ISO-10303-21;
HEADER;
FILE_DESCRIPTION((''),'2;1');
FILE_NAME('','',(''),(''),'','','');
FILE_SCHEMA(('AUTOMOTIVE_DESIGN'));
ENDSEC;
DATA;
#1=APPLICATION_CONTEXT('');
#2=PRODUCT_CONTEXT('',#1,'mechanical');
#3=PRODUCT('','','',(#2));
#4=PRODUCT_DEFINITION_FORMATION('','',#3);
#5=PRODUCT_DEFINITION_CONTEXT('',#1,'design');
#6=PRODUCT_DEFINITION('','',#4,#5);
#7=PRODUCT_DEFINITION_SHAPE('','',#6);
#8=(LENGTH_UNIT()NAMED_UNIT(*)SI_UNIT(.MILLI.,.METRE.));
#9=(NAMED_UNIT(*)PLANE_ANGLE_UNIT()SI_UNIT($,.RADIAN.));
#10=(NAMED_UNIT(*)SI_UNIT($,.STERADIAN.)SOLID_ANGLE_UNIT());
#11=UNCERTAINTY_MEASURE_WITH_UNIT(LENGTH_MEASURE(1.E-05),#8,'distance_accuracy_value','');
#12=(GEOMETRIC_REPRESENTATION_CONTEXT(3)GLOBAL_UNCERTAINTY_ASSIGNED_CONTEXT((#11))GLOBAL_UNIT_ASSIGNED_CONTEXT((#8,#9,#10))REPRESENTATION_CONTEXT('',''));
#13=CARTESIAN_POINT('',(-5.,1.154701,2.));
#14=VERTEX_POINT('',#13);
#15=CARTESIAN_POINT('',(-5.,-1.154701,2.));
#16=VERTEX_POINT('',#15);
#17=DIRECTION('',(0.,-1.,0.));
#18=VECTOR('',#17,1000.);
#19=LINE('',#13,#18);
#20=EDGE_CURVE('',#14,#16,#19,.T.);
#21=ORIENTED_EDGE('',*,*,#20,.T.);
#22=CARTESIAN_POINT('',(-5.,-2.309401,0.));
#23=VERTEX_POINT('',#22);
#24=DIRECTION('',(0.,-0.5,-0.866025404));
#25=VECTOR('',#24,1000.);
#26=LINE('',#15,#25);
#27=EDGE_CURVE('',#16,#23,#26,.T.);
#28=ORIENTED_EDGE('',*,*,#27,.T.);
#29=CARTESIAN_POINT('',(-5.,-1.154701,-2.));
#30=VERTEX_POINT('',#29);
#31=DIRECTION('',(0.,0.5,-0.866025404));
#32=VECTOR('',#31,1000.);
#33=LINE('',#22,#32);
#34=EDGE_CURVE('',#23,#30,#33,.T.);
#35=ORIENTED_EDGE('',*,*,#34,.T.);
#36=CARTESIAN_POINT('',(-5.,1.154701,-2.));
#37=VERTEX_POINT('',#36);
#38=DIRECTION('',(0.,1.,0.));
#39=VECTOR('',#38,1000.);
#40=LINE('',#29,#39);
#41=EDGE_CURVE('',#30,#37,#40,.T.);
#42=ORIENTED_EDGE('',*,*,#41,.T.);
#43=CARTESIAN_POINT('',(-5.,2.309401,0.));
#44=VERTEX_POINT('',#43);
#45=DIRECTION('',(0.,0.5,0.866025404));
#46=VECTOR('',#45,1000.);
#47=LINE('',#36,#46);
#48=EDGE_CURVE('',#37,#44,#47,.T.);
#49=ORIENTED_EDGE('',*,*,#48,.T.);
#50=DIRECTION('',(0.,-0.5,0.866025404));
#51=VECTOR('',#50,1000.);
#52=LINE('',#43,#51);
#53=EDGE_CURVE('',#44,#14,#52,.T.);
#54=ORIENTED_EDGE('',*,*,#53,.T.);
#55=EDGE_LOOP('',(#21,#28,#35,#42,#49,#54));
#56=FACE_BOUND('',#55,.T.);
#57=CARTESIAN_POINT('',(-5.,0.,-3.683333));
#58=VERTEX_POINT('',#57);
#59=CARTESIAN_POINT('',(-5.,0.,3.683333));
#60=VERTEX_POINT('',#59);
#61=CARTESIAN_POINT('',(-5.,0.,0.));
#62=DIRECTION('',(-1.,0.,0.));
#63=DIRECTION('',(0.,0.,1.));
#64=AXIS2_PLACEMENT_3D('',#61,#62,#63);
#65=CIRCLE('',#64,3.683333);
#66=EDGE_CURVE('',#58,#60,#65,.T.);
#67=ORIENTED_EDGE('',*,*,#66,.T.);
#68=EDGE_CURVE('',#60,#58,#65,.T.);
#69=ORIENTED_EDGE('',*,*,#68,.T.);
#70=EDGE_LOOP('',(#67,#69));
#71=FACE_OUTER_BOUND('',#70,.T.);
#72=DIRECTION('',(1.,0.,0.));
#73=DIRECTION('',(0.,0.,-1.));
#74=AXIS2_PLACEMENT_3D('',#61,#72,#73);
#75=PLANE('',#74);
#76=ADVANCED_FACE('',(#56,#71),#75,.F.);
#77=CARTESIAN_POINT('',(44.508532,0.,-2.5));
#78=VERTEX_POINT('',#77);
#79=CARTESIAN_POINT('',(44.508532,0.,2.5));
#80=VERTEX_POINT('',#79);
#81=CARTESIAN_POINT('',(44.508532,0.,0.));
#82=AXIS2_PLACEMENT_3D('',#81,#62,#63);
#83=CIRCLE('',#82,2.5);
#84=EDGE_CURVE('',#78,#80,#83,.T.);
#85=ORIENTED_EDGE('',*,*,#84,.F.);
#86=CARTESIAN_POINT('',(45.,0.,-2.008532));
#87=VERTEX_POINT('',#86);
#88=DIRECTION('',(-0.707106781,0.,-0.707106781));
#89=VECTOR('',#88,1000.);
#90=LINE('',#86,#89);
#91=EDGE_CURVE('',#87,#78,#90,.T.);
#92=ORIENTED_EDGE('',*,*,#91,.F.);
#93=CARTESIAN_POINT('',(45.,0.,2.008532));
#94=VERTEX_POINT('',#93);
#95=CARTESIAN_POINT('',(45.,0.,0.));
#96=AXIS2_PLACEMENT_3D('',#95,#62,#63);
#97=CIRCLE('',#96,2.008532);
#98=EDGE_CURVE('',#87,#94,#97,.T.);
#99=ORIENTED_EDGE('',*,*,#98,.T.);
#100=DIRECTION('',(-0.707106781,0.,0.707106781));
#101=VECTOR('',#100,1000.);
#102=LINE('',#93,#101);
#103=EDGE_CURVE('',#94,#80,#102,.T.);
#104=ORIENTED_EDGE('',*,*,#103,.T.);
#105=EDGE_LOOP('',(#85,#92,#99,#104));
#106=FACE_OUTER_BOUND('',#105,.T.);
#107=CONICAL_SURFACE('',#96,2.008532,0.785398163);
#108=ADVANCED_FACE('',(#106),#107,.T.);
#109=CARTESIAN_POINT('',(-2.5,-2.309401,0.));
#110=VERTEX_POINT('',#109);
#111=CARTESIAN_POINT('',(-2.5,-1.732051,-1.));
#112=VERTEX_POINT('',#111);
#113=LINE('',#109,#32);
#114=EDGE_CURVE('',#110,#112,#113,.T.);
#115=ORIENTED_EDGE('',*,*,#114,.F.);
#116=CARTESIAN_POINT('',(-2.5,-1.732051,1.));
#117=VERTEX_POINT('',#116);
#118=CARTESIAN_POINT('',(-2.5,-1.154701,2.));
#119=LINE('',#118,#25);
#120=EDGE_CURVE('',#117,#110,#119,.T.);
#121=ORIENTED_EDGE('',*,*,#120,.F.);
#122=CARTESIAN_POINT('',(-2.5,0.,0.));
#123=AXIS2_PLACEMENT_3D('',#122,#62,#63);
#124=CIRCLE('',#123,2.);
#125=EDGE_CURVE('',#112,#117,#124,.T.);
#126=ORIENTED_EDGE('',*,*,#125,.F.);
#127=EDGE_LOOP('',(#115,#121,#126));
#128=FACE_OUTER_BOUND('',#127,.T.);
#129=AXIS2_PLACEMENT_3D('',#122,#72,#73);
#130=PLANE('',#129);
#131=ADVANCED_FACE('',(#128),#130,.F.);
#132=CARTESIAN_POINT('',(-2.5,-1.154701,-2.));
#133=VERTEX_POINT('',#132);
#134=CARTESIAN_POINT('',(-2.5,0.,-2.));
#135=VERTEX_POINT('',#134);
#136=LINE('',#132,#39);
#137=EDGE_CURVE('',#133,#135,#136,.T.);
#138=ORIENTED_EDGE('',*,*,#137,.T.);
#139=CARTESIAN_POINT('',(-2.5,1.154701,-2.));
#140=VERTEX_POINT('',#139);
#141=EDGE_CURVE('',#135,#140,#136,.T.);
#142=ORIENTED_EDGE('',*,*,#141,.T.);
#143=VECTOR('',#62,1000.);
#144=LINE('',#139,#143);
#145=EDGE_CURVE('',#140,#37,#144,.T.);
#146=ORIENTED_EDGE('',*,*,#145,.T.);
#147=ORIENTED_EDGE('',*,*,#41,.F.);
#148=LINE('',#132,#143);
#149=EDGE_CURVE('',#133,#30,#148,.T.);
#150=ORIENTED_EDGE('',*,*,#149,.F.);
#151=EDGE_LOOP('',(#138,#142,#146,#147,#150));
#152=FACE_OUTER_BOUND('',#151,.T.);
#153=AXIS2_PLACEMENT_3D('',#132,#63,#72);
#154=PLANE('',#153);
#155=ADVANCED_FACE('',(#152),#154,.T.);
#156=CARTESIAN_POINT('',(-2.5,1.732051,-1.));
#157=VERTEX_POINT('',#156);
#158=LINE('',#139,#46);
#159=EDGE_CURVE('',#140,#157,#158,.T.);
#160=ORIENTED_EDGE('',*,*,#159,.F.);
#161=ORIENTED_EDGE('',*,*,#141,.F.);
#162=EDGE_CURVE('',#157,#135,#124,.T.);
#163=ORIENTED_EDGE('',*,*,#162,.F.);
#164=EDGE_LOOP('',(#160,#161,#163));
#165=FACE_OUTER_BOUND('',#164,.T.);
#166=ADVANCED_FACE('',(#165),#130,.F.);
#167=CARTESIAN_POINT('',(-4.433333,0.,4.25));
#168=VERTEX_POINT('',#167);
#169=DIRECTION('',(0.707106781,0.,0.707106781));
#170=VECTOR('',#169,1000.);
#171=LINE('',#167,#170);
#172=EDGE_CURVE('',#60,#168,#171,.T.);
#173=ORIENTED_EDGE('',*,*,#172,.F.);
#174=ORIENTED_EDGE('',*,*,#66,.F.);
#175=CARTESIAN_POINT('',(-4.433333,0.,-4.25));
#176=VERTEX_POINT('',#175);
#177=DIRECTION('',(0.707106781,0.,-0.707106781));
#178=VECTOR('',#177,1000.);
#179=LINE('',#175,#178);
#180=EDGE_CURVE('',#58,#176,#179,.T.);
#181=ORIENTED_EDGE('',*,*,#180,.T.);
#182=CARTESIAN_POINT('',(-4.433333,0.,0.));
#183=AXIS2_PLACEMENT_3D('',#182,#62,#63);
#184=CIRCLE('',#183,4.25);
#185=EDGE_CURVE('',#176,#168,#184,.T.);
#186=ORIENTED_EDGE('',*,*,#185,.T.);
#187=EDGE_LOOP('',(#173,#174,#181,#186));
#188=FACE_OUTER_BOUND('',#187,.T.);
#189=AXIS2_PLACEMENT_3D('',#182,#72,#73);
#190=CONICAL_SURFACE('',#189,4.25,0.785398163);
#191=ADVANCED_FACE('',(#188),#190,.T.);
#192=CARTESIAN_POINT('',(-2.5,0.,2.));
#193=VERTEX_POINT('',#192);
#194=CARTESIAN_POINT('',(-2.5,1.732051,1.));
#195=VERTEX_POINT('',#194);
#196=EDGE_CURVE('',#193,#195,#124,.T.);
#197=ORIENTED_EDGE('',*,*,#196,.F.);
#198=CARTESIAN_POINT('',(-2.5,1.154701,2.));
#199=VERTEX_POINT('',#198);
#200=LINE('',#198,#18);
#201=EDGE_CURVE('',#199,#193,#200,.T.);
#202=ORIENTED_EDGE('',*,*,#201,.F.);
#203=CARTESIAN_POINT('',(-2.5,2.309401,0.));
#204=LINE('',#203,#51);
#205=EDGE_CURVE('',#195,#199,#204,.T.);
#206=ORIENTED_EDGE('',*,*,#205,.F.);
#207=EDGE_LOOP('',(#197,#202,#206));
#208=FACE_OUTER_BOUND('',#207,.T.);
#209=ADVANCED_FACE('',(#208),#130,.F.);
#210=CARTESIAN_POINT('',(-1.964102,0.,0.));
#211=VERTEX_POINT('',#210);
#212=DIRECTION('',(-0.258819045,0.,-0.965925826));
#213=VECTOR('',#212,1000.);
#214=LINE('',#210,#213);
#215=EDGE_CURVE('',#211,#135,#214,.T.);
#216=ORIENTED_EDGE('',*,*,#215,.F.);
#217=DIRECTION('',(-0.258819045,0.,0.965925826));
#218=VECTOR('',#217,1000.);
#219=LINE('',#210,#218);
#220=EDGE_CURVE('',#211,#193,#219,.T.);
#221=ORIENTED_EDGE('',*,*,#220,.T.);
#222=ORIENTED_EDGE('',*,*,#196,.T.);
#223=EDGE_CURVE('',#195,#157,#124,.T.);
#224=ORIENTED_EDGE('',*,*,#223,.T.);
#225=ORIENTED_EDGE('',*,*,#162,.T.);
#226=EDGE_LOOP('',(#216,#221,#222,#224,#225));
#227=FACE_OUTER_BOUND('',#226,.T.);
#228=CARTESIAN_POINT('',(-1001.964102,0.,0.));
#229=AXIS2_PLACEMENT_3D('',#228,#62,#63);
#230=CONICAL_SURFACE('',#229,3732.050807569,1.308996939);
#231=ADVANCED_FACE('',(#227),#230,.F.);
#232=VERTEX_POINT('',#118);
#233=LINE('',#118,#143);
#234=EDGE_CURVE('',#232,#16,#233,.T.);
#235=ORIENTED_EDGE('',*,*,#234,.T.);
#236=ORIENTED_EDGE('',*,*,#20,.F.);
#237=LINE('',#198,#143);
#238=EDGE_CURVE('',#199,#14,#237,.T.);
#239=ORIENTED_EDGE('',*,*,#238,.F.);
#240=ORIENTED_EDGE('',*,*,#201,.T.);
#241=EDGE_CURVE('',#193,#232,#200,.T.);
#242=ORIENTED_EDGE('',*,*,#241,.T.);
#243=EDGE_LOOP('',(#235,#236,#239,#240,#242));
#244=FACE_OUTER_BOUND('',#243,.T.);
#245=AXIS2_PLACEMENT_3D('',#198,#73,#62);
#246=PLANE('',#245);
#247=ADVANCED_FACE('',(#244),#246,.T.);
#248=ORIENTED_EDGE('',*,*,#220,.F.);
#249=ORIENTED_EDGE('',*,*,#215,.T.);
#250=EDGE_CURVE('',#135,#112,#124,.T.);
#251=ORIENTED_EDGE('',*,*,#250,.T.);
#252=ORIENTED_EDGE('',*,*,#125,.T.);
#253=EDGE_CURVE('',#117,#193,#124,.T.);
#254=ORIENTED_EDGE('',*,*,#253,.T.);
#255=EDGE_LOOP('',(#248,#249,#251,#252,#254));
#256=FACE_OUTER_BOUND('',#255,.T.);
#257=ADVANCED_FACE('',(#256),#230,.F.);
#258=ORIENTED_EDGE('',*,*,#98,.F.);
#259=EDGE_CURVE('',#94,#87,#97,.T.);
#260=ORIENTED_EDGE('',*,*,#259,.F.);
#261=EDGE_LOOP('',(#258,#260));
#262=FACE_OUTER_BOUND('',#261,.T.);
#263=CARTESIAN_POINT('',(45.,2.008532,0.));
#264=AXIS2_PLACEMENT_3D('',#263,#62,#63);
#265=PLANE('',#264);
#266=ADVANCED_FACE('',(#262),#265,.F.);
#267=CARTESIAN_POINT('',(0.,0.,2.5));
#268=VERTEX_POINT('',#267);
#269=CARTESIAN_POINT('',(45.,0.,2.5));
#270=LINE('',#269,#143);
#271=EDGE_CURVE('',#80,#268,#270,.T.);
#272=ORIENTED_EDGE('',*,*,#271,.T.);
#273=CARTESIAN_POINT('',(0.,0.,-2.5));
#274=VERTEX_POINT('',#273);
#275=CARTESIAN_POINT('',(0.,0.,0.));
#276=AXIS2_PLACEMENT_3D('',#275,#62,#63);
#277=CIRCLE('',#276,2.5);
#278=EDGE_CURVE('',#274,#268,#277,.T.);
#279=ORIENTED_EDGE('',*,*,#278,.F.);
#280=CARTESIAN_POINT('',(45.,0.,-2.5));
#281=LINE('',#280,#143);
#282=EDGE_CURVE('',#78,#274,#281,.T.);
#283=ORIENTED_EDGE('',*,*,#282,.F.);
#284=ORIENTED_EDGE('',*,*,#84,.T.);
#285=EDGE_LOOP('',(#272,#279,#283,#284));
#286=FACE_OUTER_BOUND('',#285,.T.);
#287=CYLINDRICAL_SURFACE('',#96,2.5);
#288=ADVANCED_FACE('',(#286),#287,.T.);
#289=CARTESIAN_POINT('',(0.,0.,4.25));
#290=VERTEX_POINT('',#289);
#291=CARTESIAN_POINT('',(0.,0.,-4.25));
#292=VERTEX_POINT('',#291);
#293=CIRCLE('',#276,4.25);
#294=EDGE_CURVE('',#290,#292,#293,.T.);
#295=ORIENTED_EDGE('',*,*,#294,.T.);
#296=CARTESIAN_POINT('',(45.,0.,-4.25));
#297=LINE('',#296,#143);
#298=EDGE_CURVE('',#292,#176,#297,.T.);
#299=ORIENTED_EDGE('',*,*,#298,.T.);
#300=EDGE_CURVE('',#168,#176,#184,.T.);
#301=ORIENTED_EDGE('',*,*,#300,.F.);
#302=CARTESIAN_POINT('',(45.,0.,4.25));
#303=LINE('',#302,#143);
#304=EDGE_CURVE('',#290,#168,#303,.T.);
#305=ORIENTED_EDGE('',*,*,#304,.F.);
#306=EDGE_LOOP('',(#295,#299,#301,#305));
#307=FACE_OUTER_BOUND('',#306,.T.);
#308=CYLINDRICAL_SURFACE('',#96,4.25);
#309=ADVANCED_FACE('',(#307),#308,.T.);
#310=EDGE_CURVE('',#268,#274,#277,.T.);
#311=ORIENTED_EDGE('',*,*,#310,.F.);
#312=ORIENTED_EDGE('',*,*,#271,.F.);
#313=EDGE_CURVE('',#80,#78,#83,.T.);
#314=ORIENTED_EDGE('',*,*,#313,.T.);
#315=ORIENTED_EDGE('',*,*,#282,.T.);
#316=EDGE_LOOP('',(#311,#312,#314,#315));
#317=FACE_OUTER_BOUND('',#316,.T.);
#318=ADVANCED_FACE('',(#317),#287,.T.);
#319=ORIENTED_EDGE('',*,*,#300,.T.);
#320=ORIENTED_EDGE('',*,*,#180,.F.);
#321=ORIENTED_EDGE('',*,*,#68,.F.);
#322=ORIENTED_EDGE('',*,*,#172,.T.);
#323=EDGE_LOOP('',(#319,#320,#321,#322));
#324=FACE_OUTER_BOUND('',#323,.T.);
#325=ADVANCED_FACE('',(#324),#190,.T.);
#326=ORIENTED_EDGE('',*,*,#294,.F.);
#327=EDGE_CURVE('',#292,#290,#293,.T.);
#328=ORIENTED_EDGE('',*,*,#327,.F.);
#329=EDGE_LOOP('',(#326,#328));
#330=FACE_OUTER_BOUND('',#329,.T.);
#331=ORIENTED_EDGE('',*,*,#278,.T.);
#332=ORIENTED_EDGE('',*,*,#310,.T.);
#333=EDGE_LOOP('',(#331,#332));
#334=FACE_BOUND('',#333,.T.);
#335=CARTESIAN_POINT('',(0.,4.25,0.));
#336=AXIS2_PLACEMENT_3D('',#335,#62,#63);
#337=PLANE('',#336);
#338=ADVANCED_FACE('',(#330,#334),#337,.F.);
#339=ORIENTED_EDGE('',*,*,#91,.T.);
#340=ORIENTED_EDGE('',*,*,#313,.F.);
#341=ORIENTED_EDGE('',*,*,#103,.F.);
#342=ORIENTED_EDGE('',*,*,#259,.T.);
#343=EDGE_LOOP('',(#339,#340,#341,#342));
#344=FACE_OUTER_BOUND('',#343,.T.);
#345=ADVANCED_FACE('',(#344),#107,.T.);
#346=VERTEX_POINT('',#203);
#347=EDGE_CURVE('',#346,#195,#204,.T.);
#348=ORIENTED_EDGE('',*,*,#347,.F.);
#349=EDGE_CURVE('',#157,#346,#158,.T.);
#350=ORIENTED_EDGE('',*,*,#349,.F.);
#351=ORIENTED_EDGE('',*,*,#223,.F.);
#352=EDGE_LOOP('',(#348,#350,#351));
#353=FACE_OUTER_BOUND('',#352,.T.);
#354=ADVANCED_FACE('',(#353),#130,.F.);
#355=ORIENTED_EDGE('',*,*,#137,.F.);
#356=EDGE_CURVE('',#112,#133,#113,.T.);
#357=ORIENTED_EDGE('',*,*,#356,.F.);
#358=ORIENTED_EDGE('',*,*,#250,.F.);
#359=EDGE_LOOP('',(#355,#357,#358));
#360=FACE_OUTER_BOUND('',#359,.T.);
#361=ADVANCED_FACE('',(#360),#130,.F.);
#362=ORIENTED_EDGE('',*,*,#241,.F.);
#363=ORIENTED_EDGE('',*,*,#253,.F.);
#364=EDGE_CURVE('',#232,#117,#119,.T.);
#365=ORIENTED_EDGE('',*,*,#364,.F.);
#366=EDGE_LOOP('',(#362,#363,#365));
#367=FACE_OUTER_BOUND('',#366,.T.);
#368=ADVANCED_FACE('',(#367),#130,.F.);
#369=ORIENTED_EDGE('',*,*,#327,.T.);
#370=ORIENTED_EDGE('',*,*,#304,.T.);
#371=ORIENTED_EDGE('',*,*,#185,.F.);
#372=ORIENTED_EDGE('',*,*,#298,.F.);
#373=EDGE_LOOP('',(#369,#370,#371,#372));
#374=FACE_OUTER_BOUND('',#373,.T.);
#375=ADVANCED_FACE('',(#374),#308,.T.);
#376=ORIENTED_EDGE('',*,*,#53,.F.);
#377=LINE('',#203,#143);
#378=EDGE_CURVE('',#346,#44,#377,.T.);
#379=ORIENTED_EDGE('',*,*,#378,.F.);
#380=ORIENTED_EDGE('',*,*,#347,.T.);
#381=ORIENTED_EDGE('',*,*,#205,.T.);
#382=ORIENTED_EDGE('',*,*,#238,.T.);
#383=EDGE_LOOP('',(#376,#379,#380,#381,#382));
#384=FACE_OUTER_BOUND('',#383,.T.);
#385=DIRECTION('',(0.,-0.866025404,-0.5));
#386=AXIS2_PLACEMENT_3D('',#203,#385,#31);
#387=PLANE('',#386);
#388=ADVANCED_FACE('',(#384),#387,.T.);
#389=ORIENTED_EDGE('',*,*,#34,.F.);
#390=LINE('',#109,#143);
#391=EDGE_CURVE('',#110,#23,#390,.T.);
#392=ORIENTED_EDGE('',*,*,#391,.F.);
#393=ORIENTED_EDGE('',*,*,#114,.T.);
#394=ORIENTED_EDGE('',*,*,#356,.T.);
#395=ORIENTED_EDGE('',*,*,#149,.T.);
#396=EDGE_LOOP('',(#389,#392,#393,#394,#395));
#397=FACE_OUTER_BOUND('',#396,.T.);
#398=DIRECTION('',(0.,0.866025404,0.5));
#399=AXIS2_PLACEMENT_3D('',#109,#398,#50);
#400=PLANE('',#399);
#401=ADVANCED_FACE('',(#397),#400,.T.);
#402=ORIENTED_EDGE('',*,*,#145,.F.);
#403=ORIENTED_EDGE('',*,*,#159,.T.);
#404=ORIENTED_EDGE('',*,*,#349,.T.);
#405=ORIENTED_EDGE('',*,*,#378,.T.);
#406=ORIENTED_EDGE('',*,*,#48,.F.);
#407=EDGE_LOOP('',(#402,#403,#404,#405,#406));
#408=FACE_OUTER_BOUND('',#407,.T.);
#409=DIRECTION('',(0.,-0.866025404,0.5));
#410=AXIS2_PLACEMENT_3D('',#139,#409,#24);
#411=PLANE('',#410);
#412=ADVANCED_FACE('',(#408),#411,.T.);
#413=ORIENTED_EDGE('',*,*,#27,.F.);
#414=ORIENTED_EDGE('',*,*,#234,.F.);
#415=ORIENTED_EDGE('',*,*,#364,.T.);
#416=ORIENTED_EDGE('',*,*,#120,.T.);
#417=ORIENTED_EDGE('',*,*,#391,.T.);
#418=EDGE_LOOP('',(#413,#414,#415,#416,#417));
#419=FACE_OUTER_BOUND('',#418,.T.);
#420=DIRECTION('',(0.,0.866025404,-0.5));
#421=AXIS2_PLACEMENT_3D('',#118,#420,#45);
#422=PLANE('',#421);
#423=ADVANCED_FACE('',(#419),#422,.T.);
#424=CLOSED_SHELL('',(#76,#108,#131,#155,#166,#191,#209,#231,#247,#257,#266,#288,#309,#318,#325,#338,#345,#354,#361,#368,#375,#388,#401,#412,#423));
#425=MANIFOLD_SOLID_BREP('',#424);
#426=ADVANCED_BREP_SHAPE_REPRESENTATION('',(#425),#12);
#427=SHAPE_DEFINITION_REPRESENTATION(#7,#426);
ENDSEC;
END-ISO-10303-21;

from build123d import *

# Parameters (mm, degrees)
CUT_EXTRUDE1_DEPTH = 2.5


with BuildPart() as part:
    # Sketch1 → Revolve1 (revolve)
    with BuildSketch(Plane.XY, mode=Mode.PRIVATE) as revolve1_sk:
        Polygon((-5, 0), (-5, 3.683333333), (-4.433333333, 4.25), (0, 4.25), (0, 2.5), (44.508532, 2.5), (45, 2.008532), (45, 0), align=None)
    revolve(revolve1_sk.sketch.rotate(Axis((45, 0, 0), (-1, 0, 0)), 270), axis=Axis((45, 0, 0), (-1, 0, 0)))

    # Sketch2 → Cut-Revolve1 (revolve, cut)
    with BuildSketch(Plane.XY, mode=Mode.PRIVATE) as cut_revolve1_sk:
        Polygon((-5, 0), (-5, 2), (-2.5, 2), (-1.964101615, 0), align=None)
    revolve(cut_revolve1_sk.sketch.rotate(Axis((-1.964101615, 0, 0), (-1, 0, 0)), 270), axis=Axis((-1.964101615, 0, 0), (-1, 0, 0)), mode=Mode.SUBTRACT)

    # Sketch3 → Cut-Extrude1 (cut)
    with BuildSketch(Plane(origin=(-5, 0, 0), x_dir=(0, 0, -1), z_dir=(1, 0, 0))):
        Polygon((-2, 1.154700538), (-2, -1.154700538), (0, -2.309401077), (2, -1.154700538), (2, 1.154700538), (0, 2.309401077), align=None)
    extrude(amount=CUT_EXTRUDE1_DEPTH, mode=Mode.SUBTRACT)


solid = part.part
